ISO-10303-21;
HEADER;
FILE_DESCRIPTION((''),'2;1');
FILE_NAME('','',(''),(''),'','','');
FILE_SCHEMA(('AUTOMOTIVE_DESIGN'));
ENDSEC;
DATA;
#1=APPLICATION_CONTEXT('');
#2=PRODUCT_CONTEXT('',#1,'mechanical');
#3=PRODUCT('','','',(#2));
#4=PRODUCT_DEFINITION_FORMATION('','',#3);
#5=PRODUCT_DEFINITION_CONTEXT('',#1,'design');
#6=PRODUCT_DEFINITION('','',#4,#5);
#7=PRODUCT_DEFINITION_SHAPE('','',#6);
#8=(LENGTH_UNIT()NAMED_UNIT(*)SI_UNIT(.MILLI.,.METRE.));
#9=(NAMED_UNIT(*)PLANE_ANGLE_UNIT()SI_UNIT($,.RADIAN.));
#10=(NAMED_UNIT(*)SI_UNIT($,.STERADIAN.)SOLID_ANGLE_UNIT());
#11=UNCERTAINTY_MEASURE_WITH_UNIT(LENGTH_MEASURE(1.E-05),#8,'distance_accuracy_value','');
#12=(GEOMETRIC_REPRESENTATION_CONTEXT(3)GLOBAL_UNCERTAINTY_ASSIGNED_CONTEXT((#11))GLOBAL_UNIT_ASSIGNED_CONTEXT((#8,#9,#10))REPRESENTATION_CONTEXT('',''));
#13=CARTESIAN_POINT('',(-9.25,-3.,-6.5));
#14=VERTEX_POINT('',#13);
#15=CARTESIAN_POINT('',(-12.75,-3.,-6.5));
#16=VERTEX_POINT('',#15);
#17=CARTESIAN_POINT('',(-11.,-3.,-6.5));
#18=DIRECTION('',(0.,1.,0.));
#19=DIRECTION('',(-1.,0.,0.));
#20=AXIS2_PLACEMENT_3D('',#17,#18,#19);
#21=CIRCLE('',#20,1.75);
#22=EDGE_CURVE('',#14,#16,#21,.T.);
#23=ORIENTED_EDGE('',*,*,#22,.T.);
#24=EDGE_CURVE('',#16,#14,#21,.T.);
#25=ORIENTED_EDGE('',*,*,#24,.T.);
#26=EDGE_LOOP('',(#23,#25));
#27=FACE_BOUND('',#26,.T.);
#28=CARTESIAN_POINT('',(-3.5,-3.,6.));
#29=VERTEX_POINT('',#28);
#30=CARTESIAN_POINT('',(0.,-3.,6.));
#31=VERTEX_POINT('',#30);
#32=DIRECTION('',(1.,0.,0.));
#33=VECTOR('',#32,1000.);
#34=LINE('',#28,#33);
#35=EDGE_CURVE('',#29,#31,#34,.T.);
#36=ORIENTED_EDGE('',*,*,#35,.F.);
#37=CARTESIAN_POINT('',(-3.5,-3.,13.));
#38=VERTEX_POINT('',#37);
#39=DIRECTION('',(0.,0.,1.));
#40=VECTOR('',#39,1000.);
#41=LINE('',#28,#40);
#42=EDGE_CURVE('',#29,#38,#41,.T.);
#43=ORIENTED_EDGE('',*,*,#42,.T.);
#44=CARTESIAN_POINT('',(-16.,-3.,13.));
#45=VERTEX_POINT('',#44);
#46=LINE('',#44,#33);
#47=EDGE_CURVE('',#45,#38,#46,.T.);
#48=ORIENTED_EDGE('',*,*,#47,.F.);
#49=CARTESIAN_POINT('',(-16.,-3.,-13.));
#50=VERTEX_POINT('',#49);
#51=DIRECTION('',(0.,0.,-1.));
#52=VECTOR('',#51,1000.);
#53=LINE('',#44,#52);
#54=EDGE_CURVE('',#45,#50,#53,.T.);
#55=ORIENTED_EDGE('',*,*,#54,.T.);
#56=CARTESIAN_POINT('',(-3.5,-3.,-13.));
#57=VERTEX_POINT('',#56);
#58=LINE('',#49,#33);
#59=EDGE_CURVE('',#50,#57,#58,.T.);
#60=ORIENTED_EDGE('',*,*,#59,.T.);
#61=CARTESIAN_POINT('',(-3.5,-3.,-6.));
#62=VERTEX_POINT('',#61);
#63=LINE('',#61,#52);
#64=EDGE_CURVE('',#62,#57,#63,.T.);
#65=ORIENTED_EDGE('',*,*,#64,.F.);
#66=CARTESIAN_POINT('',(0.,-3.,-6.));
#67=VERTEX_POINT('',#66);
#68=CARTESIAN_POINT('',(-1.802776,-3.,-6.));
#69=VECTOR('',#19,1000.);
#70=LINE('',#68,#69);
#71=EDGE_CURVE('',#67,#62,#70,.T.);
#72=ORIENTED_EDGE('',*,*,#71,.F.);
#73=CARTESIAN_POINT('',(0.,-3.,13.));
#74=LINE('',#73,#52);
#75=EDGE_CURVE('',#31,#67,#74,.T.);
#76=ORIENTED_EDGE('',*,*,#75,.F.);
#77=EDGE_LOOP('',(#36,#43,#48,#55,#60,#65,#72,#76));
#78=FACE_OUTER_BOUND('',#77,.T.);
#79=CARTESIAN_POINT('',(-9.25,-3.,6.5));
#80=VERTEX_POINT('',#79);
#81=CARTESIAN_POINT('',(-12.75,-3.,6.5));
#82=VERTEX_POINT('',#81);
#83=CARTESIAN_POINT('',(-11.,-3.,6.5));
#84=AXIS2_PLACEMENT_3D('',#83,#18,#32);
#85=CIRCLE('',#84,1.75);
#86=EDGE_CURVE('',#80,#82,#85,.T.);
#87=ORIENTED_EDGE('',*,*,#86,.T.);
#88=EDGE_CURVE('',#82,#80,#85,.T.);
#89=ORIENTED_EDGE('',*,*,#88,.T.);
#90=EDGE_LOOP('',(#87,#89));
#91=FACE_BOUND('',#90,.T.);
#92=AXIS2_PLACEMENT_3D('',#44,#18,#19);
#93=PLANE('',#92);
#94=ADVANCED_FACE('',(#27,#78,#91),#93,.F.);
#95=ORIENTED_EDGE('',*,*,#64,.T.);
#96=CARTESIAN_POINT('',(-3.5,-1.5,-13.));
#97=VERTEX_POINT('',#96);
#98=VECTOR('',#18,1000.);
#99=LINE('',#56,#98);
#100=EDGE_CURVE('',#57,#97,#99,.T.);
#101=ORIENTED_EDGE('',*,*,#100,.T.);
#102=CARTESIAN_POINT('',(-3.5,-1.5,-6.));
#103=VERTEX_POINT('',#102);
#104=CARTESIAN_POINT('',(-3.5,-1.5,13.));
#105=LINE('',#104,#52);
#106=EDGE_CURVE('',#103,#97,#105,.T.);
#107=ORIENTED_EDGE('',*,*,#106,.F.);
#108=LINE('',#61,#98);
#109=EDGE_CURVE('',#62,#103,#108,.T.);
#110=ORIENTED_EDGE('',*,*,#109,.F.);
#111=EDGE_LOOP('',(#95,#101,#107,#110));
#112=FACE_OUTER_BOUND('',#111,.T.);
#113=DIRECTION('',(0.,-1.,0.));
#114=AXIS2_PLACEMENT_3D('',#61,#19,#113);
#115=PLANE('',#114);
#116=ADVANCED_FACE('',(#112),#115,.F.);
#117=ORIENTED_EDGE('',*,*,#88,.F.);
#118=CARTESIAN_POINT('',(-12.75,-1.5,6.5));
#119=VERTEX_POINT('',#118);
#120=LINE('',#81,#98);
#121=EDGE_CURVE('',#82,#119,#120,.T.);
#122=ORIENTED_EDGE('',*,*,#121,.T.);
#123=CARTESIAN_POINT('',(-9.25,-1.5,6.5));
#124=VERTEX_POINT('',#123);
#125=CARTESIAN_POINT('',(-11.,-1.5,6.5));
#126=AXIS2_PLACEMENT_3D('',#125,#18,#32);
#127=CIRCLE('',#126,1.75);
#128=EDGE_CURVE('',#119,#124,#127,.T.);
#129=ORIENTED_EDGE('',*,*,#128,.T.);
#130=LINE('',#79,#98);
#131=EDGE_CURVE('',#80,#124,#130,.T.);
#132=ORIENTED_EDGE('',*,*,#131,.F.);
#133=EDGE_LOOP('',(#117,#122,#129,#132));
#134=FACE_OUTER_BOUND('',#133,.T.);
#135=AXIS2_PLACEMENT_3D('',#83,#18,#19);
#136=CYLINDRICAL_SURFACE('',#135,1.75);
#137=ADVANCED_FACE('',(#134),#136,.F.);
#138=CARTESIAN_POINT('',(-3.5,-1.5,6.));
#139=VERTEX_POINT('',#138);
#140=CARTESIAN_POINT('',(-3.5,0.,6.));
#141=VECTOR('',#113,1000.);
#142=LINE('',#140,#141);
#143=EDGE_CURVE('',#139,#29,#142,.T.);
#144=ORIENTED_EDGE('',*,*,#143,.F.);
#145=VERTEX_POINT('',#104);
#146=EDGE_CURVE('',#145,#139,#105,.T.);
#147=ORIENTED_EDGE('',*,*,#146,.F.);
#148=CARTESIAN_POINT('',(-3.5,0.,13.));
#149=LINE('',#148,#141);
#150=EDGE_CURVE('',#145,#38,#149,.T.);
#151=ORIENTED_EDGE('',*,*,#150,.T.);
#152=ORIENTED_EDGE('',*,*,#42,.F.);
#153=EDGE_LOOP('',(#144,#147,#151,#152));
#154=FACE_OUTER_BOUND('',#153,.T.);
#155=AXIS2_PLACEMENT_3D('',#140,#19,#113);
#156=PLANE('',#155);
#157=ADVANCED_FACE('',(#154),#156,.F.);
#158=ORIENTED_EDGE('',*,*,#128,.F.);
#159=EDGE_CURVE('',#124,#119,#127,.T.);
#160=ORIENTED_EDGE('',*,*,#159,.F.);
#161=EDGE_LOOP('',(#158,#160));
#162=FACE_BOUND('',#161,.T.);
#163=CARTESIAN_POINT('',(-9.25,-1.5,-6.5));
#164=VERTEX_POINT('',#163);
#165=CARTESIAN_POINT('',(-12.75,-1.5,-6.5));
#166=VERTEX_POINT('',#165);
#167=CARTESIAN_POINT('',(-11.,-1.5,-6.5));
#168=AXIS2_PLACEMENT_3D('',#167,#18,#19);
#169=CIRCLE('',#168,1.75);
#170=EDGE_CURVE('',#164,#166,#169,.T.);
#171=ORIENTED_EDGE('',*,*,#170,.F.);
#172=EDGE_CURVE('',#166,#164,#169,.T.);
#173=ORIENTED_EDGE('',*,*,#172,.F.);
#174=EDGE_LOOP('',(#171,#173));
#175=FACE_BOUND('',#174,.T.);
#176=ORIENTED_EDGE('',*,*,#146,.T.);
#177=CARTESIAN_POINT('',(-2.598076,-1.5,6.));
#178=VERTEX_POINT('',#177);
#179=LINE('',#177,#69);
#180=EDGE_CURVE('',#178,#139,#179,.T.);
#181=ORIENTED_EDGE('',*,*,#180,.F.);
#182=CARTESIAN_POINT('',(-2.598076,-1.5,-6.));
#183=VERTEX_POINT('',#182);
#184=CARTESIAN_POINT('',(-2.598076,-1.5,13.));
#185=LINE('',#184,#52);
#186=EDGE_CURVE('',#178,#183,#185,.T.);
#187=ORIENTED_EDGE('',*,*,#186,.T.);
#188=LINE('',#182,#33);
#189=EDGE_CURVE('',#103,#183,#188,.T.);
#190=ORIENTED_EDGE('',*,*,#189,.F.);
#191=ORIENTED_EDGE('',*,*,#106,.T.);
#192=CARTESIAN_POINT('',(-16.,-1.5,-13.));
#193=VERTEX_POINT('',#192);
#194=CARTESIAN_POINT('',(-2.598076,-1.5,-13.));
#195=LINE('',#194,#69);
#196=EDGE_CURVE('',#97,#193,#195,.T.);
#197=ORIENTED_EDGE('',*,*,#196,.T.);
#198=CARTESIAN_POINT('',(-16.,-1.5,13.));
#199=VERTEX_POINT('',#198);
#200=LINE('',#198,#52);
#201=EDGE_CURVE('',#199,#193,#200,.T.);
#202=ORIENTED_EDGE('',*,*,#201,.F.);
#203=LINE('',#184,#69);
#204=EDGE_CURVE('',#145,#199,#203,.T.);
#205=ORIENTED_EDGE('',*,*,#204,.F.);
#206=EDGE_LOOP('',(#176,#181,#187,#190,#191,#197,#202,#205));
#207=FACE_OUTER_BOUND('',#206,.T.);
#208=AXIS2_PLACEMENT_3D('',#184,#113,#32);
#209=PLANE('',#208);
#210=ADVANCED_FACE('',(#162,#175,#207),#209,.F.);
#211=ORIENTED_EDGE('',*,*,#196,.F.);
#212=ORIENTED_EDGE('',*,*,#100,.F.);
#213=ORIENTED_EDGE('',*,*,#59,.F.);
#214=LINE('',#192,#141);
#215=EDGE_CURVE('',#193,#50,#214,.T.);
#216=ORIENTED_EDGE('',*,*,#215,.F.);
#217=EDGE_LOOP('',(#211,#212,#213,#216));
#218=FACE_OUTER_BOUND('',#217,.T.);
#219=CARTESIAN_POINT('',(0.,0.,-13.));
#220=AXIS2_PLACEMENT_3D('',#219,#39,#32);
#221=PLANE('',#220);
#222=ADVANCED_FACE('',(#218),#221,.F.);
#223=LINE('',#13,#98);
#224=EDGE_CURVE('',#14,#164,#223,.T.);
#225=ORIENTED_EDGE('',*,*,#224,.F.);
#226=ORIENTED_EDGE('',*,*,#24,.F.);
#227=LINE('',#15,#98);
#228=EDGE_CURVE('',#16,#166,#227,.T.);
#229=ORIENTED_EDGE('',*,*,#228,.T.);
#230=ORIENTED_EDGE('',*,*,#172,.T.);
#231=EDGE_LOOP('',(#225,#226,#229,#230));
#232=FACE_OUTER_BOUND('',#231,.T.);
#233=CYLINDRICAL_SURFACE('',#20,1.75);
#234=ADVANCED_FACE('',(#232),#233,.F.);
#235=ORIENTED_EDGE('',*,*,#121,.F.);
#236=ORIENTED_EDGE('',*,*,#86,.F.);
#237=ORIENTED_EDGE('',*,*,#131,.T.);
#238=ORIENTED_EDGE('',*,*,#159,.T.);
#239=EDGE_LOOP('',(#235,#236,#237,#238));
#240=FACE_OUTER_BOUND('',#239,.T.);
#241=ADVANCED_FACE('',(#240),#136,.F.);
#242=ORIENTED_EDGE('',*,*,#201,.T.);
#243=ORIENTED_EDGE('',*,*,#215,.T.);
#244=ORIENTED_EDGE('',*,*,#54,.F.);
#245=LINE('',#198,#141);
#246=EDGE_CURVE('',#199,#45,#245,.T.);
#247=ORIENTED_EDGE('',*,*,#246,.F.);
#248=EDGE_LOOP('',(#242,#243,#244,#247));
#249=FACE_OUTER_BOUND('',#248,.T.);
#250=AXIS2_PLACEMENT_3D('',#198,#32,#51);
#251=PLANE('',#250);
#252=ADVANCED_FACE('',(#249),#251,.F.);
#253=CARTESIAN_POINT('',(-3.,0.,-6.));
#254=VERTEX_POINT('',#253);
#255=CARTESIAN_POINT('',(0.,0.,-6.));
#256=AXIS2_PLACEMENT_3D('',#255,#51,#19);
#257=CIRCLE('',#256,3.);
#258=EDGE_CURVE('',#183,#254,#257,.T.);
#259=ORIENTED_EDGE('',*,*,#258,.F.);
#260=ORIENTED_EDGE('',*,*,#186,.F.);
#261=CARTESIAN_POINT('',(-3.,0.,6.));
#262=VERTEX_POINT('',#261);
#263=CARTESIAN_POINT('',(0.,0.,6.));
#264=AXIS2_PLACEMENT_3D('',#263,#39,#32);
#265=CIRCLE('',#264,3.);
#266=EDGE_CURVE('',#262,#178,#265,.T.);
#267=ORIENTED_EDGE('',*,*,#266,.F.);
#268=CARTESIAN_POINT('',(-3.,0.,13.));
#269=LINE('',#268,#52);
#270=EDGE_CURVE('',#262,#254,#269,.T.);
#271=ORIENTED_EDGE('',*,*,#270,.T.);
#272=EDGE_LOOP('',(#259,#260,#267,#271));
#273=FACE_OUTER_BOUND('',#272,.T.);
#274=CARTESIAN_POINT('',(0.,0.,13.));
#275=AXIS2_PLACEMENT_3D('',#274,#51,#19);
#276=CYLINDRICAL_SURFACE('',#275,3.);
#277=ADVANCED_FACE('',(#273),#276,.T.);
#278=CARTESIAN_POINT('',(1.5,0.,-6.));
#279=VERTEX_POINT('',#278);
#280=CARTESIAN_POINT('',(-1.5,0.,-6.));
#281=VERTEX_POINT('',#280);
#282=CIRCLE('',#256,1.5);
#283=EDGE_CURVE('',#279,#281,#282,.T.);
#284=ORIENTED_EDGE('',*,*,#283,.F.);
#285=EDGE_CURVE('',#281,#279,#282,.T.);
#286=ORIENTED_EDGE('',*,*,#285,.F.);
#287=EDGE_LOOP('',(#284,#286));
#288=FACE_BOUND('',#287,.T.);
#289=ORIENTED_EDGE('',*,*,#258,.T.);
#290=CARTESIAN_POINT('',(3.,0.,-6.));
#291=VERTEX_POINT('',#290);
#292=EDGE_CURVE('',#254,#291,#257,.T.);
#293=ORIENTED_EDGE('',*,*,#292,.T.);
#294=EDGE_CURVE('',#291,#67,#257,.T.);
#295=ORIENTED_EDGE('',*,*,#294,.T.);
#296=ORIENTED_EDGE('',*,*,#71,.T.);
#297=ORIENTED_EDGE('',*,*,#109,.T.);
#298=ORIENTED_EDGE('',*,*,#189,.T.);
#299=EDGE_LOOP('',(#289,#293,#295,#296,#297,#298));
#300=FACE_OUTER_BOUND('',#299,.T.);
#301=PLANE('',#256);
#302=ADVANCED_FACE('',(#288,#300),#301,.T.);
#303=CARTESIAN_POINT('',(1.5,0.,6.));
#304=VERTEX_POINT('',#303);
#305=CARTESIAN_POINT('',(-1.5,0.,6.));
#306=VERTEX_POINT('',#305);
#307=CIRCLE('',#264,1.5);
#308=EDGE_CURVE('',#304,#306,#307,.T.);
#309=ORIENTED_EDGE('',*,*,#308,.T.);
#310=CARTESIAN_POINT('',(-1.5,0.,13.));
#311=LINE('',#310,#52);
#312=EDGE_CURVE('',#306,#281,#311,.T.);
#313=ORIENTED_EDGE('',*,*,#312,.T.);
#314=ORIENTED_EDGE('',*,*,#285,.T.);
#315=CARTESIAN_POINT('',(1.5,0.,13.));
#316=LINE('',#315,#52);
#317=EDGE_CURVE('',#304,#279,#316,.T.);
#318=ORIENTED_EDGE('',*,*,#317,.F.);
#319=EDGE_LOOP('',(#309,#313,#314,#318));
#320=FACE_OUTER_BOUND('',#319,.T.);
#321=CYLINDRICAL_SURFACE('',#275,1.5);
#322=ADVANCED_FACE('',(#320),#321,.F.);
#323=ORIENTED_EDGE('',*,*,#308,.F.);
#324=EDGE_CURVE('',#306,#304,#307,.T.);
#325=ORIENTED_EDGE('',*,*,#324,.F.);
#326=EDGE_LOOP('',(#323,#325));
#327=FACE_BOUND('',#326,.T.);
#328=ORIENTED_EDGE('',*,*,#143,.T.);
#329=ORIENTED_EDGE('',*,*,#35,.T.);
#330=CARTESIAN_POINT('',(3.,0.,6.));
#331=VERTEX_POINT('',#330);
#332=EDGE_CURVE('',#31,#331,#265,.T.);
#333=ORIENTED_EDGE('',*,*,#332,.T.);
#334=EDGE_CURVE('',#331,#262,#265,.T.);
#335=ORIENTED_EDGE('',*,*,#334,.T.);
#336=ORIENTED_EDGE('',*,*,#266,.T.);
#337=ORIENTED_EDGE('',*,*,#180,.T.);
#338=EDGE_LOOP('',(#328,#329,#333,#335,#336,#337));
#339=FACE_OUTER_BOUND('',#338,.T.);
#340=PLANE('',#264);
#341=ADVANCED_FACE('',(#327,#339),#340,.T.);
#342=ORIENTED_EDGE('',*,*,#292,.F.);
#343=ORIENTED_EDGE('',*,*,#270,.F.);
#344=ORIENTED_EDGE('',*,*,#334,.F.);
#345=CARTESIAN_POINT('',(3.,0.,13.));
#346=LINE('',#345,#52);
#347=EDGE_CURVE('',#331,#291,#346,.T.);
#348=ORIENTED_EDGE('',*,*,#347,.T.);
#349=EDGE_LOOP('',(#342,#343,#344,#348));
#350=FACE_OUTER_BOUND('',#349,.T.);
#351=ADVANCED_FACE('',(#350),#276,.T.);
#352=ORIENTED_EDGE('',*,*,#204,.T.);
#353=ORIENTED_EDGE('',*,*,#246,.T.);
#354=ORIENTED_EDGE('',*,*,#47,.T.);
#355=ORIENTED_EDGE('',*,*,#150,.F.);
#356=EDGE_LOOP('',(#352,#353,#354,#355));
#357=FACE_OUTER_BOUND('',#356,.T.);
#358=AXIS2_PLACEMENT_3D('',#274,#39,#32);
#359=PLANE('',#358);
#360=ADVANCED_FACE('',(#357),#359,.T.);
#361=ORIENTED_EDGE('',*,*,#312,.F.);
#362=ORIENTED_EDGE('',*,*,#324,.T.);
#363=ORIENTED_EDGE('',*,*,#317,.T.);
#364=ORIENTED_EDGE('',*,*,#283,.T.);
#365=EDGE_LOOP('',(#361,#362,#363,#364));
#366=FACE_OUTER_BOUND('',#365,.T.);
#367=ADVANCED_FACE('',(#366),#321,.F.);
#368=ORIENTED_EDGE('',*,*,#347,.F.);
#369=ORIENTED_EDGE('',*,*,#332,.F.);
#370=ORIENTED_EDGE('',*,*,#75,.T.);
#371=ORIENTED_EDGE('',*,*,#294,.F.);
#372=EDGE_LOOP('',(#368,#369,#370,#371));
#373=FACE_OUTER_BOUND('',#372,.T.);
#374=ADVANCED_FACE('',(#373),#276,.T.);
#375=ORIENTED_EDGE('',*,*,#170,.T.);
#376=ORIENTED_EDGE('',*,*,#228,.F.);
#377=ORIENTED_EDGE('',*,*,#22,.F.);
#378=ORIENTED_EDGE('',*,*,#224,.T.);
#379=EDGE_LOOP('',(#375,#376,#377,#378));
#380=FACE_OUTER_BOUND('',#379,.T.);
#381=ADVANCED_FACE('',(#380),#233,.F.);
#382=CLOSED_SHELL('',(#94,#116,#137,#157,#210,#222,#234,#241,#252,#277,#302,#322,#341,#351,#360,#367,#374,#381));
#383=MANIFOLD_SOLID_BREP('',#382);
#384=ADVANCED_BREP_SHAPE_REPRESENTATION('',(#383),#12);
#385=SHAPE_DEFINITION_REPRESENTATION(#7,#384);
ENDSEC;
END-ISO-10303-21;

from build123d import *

# Parameters (mm, degrees)
SKETCH_1_R          = 1.5
EXTRUDE_1_DEPTH     = 13
CUT_EXTRUDE_3_DEPTH = 7
CUT_EXTRUDE_4_DEPTH = 7
SKETCH_3_R          = 1.75
CUT_EXTRUDE_2_DEPTH = 22.100947846


with BuildPart() as part:
    # 草图1 → 凸台-拉伸1 (new, symmetric)
    with BuildSketch(Plane.XY):
        with BuildLine():
            Line((-2.598076211, -1.5), (-16, -1.5))
            Line((-16, -1.5), (-16, -3))
            Line((-16, -3), (0, -3))
            ThreePointArc((0, -3), (1.5, 2.598076211), (-2.598076211, -1.5))
        make_face()
        with Locations(Location((0, 0, 0), (0, 0, 180))):
            Circle(SKETCH_1_R, mode=Mode.SUBTRACT)
    extrude(amount=EXTRUDE_1_DEPTH, both=True)

    # 草图2 → 切除-拉伸3 (cut)
    with BuildSketch(Plane.XY.offset(13)):
        with BuildLine():
            Line((-3.5, 0), (-3.5, -3))
            Line((-3.5, -3), (-1.802775638, -3))
            ThreePointArc((-1.802775638, -3), (3.046285831, 1.723410176), (-3.5, 0))
        make_face()
    extrude(amount=-CUT_EXTRUDE_3_DEPTH, mode=Mode.SUBTRACT)

    # 草图4 → 切除-拉伸4 (cut)
    with BuildSketch(Plane(origin=(0, 0, -13), x_dir=(-1, 0, 0), z_dir=(0, 0, -1))):
        with BuildLine():
            Line((3.5, -3), (3.5, 0))
            ThreePointArc((3.5, 0), (-3.046285831, 1.723410176), (1.802775638, -3))
            Line((1.802775638, -3), (3.5, -3))
        make_face()
    extrude(amount=-CUT_EXTRUDE_4_DEPTH, mode=Mode.SUBTRACT)

    # 草图3 → 切除-拉伸2 (cut, through all)
    with BuildSketch(Plane(origin=(0, -1.5, 0), x_dir=(1, 0, 0), z_dir=(0, 1, 0))):
        with Locations(Location((-11, 6.5, 0), (0, 0, 180))):
            Circle(SKETCH_3_R)
        with Locations((-11, -6.5)):
            Circle(SKETCH_3_R)
    extrude(amount=-CUT_EXTRUDE_2_DEPTH, mode=Mode.SUBTRACT)


solid = part.part
